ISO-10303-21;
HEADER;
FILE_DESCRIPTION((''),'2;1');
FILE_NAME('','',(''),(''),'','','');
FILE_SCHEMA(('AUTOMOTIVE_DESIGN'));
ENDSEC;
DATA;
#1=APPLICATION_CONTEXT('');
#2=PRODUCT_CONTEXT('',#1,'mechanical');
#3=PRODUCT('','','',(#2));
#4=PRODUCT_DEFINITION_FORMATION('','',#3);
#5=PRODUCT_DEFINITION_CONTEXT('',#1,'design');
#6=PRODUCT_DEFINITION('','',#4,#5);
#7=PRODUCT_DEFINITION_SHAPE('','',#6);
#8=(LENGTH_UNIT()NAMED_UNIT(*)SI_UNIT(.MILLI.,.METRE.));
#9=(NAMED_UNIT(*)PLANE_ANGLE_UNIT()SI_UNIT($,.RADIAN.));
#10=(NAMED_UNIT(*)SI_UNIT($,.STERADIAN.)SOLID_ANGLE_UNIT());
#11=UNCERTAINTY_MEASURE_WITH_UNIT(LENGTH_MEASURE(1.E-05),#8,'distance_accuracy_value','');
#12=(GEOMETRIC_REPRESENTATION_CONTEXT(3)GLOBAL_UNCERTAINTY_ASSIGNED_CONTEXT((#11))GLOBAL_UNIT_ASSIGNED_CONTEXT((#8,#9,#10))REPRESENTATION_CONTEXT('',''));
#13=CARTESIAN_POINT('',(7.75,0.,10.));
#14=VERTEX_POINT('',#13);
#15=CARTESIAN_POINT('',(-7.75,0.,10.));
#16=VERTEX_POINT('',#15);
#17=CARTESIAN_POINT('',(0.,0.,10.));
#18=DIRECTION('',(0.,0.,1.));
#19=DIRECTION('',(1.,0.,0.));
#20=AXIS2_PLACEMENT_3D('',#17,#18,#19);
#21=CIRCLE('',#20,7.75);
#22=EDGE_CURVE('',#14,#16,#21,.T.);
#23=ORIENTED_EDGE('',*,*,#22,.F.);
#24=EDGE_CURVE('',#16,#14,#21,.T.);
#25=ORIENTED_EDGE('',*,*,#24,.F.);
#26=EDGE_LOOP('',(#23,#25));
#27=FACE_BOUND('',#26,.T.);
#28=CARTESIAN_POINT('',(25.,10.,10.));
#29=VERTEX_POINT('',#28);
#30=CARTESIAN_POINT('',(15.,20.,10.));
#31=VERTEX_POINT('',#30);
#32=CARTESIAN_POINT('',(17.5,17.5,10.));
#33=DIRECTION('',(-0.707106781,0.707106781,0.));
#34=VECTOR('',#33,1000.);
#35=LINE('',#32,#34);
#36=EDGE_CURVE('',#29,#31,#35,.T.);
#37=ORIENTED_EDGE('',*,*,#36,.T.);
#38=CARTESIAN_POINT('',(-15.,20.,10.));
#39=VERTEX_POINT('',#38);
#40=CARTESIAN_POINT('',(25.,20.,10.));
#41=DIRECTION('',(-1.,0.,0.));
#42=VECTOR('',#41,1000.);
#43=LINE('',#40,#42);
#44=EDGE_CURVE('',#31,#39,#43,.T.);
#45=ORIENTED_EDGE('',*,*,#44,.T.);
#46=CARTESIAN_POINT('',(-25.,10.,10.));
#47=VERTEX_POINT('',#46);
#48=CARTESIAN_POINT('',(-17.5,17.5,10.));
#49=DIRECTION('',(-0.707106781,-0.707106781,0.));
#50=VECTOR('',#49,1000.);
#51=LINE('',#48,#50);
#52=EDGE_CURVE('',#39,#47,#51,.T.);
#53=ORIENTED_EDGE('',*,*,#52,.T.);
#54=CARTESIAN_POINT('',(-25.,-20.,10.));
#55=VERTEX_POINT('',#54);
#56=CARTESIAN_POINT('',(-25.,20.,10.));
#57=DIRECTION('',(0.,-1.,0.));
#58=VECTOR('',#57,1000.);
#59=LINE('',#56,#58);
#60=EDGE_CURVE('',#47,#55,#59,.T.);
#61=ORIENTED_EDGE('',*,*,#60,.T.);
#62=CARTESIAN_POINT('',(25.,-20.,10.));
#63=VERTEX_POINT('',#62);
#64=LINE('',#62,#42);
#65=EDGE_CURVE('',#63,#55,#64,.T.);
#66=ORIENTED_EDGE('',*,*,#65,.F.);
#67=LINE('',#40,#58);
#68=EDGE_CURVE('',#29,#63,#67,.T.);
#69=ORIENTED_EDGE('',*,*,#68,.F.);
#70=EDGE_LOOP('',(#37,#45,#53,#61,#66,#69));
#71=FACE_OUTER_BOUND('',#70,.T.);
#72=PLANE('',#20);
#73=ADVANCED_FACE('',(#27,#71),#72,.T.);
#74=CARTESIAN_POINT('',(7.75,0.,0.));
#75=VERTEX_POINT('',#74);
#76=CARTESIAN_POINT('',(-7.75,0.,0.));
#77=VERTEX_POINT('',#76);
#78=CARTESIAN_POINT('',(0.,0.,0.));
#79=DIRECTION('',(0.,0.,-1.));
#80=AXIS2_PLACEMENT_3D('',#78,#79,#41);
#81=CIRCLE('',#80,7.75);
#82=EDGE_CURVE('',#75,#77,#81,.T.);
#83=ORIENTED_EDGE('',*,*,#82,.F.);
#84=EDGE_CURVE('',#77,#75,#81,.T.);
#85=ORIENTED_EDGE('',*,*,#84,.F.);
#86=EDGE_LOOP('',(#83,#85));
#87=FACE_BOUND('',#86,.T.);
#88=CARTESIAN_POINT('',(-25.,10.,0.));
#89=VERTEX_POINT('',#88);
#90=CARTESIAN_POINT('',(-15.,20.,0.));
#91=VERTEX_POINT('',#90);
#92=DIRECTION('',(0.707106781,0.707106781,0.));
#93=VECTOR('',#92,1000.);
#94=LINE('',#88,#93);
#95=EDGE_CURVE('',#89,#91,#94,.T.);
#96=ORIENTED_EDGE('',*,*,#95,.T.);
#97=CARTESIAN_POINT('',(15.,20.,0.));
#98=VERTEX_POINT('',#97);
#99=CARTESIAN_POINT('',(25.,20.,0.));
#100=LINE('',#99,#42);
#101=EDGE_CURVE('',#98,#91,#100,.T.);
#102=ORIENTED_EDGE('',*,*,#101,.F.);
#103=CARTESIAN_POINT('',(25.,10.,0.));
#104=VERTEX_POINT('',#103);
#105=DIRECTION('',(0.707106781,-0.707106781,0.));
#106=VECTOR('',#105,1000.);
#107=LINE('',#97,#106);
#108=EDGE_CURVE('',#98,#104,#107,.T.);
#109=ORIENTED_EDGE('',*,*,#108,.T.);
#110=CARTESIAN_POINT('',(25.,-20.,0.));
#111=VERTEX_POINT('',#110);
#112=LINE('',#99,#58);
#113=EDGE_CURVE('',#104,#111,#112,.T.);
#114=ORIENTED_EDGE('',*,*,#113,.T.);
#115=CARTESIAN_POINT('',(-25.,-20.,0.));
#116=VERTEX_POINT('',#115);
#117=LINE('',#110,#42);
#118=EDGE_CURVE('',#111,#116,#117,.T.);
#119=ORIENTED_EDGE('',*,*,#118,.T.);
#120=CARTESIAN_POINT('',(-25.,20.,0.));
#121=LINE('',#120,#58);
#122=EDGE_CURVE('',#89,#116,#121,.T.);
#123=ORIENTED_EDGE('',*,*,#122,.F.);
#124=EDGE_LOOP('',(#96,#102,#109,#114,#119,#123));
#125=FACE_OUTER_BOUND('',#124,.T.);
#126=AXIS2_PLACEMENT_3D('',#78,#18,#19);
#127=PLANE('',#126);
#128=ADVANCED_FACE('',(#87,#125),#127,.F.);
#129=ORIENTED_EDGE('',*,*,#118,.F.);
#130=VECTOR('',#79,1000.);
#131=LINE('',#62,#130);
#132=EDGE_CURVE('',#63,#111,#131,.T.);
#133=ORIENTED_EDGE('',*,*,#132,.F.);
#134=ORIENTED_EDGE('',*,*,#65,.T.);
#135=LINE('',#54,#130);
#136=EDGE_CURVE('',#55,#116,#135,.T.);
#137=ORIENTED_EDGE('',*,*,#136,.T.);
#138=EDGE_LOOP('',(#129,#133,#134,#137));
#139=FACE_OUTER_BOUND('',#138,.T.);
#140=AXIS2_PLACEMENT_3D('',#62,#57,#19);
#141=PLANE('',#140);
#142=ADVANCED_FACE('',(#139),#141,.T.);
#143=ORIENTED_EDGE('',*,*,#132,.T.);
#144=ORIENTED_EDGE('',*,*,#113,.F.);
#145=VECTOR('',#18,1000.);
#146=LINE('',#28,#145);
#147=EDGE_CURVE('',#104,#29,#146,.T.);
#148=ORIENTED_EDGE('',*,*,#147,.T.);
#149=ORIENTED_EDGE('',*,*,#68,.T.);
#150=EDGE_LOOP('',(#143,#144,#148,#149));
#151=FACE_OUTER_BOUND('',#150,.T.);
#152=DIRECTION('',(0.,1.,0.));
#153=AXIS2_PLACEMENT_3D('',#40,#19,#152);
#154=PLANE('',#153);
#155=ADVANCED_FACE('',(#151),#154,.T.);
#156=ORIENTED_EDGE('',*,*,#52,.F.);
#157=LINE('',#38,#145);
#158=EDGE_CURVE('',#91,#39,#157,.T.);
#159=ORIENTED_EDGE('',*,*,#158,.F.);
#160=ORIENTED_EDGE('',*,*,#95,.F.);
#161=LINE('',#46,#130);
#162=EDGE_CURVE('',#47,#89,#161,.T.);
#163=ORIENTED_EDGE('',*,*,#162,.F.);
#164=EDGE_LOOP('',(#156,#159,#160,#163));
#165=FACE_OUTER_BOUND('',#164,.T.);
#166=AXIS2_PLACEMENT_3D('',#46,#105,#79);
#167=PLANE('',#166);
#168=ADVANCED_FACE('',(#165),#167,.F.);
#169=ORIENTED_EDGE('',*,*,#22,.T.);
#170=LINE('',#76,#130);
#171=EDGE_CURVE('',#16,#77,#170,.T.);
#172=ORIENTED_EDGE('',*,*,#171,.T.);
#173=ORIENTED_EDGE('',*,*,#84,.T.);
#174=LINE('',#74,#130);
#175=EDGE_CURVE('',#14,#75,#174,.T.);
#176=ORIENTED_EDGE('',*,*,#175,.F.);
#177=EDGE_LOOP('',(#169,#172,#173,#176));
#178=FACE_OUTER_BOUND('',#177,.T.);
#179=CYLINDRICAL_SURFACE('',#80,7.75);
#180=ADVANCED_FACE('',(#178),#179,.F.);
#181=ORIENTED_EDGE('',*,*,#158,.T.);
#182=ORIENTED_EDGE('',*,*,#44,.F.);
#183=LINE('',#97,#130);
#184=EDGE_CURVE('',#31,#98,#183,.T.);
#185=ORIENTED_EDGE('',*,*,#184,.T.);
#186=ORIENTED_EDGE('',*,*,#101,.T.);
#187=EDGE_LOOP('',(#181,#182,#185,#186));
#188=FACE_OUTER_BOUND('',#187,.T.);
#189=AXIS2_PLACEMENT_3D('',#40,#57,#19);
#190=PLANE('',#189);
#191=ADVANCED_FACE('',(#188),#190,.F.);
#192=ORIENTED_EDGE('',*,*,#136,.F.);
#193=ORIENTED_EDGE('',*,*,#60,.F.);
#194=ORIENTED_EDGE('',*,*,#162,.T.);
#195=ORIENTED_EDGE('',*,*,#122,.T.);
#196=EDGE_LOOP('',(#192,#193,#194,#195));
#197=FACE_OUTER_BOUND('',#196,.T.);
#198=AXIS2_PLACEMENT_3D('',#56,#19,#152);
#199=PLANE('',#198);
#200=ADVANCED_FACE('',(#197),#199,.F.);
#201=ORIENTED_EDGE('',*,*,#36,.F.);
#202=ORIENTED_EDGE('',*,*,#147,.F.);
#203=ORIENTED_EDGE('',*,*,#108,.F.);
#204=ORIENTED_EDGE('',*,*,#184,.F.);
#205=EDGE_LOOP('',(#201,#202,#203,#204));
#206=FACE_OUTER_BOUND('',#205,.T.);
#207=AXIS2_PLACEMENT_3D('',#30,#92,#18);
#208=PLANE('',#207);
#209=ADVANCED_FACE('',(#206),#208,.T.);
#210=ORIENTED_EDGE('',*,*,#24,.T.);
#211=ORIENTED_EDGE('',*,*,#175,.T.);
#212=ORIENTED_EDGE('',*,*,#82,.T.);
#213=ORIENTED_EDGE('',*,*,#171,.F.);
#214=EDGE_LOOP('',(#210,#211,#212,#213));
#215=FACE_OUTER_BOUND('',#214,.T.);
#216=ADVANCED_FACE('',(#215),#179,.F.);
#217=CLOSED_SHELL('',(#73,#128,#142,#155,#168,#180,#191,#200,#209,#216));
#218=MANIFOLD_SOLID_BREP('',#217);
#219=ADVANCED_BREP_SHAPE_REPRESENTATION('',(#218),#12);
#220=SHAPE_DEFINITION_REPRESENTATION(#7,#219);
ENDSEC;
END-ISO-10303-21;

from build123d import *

# Parameters (mm, degrees)
SKETCH1_W              = 50
SKETCH1_H              = 40
BOSS_EXTRUDE1_DEPTH    = 10
CHAMFER1_SIZE          = 10
M18_TAPPED_HOLE1_D     = 15.5
M18_TAPPED_HOLE1_DEPTH = 43.5
M18_TAPPED_HOLE1_TIP   = 4.656669797


with BuildPart() as part:
    # Sketch1 → Boss-Extrude1 (new body)
    with BuildSketch(Plane.XY):
        Rectangle(SKETCH1_W, SKETCH1_H)
    extrude(amount=BOSS_EXTRUDE1_DEPTH)

    # Chamfer1
    chamfer1_edges = [part.edges().sort_by_distance(p)[0] for p in [
        (25, 20, 5),
        (-25, 20, 5),
    ]]
    chamfer(chamfer1_edges, length=CHAMFER1_SIZE)

    # M18 Tapped Hole1
    with Locations(Plane(origin=(0, 0, 0), x_dir=(-1, 0, 0), z_dir=(0, 0, -1))):
        with Locations((0, 0)):
            Hole(M18_TAPPED_HOLE1_D / 2, depth=M18_TAPPED_HOLE1_DEPTH)
            with Locations((0, 0, -(M18_TAPPED_HOLE1_DEPTH + M18_TAPPED_HOLE1_TIP / 2))):  # 118° drill point
                Cone(0, M18_TAPPED_HOLE1_D / 2, M18_TAPPED_HOLE1_TIP, mode=Mode.SUBTRACT)


solid = part.part
